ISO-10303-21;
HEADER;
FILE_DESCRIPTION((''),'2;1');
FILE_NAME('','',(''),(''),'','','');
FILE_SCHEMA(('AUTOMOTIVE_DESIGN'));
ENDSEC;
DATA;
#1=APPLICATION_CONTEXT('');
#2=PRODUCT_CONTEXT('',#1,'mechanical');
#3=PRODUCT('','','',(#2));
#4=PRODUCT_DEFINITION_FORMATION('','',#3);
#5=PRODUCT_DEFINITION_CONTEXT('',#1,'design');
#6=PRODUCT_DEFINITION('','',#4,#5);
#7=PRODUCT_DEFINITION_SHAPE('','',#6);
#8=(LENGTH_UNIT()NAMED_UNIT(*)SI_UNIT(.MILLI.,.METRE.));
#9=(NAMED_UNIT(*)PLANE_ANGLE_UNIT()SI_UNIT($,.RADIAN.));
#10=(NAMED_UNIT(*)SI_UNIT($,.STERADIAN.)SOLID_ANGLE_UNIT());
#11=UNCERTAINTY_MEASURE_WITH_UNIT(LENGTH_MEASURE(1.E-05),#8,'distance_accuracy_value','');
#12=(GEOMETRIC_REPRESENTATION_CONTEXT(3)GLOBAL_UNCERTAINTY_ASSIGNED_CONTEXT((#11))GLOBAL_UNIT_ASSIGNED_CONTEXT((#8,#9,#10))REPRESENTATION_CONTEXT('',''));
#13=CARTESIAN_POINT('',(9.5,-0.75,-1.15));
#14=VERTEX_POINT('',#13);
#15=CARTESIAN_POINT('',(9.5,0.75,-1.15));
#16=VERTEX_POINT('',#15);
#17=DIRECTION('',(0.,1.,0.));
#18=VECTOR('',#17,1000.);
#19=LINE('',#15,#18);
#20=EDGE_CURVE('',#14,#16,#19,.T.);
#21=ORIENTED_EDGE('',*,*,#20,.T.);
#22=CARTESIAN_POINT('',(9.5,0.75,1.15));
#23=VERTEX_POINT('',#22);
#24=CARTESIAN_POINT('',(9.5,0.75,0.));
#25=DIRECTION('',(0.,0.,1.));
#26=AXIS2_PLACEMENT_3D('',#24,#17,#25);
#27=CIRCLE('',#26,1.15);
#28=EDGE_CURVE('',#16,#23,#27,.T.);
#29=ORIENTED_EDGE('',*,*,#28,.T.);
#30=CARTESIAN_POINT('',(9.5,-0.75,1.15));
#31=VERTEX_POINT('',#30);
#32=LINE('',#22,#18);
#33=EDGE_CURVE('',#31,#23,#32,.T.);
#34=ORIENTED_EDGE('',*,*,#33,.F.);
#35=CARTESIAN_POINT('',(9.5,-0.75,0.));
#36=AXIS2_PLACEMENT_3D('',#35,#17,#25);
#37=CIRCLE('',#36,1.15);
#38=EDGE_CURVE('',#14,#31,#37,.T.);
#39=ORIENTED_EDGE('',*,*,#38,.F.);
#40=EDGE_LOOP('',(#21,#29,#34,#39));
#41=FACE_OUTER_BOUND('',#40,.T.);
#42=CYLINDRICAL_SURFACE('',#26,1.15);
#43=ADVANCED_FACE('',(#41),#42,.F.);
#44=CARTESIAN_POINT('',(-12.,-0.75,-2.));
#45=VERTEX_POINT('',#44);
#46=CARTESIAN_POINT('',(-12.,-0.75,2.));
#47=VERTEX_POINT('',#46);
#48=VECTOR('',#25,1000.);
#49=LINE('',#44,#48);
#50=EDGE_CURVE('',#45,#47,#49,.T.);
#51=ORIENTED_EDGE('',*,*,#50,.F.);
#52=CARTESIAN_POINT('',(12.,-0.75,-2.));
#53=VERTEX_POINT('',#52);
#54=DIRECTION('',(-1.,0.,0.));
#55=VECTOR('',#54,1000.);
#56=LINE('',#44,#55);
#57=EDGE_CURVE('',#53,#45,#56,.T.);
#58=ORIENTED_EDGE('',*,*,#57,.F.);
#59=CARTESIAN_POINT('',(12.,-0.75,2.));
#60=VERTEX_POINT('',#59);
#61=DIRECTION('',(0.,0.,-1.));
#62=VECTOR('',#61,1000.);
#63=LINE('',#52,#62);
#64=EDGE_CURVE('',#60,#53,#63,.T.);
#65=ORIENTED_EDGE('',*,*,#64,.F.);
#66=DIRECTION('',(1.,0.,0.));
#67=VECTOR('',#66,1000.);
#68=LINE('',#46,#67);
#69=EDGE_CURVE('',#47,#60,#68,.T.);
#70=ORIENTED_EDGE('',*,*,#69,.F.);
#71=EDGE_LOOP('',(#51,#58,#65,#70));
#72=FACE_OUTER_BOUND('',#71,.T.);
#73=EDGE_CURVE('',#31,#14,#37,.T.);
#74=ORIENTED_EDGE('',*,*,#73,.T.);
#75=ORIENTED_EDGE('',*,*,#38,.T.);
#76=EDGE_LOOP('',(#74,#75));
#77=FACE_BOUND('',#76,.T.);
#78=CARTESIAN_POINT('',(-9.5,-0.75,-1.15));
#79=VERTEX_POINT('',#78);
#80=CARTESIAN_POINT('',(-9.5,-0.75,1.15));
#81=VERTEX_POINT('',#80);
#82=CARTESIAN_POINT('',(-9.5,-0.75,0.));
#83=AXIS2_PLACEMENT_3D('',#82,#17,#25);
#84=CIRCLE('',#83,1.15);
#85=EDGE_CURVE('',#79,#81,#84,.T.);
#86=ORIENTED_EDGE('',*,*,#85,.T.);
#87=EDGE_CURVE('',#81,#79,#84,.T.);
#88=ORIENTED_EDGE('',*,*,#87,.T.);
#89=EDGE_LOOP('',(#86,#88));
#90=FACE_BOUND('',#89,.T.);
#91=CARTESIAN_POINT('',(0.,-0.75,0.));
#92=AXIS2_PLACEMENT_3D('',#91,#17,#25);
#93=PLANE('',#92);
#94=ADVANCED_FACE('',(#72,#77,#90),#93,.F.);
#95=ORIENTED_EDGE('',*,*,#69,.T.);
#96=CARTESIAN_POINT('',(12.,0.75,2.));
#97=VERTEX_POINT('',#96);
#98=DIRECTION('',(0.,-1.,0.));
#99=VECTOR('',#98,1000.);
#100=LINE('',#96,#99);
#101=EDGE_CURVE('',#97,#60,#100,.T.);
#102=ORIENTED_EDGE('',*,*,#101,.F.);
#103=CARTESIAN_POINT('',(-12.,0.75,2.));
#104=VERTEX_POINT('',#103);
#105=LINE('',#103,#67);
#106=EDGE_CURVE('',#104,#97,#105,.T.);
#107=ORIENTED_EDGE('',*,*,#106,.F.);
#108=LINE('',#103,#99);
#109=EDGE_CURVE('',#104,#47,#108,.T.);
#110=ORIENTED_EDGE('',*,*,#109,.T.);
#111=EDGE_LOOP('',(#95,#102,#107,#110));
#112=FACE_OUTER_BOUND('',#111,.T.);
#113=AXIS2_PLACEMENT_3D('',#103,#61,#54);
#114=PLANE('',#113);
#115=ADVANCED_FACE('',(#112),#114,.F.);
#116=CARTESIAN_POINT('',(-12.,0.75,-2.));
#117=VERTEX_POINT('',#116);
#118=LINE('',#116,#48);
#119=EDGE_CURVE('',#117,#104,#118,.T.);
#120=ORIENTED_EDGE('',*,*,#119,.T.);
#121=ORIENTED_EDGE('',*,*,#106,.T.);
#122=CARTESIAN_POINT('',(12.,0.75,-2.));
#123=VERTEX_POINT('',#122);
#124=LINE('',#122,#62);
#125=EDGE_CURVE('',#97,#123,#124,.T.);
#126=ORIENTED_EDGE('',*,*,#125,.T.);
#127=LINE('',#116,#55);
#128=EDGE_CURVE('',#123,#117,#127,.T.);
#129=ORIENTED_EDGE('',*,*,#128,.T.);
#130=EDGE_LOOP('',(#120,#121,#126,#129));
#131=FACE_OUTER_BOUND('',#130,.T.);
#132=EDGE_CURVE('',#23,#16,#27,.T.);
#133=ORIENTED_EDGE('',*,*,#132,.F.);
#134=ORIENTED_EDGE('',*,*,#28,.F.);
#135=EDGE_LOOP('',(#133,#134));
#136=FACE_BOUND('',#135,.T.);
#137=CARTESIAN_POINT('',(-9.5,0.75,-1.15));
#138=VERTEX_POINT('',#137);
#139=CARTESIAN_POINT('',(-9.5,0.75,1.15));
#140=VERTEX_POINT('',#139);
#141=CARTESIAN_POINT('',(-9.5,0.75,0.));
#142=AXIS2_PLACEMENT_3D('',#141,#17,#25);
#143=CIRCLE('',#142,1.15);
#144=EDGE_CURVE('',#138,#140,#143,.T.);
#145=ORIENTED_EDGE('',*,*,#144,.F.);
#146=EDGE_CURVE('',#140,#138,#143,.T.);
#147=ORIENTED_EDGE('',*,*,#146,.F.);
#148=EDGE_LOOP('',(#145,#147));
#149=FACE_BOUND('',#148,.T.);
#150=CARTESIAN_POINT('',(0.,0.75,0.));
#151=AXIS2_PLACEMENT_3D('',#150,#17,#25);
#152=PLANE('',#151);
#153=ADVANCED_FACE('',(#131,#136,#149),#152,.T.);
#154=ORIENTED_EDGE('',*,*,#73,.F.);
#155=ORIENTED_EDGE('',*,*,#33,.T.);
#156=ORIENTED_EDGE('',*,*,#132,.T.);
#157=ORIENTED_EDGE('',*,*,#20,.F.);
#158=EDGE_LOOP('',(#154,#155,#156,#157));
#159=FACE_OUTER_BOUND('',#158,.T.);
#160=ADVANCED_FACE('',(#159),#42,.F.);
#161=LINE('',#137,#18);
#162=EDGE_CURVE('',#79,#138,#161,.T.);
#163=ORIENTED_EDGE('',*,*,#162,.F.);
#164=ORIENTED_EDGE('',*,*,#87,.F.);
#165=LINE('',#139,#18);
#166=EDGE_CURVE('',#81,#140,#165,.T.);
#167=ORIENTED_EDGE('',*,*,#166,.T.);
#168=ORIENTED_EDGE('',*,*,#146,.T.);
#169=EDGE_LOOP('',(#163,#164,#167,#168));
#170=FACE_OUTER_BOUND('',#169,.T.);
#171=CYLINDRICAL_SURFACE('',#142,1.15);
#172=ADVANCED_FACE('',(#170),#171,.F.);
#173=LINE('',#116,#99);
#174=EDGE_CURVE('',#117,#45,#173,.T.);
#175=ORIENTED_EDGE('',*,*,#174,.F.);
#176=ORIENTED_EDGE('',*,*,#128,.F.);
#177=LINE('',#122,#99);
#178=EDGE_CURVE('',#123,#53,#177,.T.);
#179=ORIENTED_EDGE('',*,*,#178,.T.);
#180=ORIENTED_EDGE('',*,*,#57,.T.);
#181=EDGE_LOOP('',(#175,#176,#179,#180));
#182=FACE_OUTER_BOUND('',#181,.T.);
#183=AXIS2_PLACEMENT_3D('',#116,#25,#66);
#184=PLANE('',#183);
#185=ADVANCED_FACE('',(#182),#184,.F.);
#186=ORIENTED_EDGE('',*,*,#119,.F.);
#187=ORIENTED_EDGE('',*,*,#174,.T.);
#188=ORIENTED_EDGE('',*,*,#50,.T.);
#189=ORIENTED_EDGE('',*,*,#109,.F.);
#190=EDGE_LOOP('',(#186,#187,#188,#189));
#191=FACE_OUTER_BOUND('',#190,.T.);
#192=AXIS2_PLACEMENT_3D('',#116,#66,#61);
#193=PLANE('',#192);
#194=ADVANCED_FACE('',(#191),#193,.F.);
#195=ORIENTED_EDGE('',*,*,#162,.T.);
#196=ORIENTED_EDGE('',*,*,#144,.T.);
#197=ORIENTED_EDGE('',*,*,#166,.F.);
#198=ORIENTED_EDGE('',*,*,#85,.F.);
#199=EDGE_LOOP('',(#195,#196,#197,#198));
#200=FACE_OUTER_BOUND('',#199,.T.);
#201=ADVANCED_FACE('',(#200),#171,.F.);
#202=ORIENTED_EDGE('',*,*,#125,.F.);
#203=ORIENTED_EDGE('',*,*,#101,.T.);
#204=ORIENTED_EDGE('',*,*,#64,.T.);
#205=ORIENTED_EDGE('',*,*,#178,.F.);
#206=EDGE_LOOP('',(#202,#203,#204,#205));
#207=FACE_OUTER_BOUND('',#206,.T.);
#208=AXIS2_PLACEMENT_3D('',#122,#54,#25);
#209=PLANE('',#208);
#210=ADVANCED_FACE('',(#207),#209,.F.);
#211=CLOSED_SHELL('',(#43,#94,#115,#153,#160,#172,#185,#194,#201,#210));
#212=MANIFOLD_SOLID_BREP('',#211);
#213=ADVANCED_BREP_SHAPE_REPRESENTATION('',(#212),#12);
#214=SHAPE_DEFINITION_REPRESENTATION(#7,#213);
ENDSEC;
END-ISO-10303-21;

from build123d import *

# Parameters (mm, degrees)
SKETCH1_W                  = 24
SKETCH1_H                  = 4
BOSS_EXTRUDE1_DEPTH        = 0.75
F_2_3_2_3_DIAMETER_HOLE1_D = 2.3


with BuildPart() as part:
    # Sketch1 → Boss-Extrude1 (new, symmetric)
    with BuildSketch(Plane(origin=(0, 0, 0), x_dir=(1, 0, 0), z_dir=(0, 1, 0))):
        Rectangle(SKETCH1_W, SKETCH1_H)
    extrude(amount=BOSS_EXTRUDE1_DEPTH, both=True)

    # Ø2.3 (2.3) Diameter Hole1 (through all)
    with Locations(Plane(origin=(0, 0.75, 0), x_dir=(1, 0, 0), z_dir=(0, 1, 0))):
        with Locations((-9.5, 0), (9.5, 0)):
            Hole(F_2_3_2_3_DIAMETER_HOLE1_D / 2)


solid = part.part
